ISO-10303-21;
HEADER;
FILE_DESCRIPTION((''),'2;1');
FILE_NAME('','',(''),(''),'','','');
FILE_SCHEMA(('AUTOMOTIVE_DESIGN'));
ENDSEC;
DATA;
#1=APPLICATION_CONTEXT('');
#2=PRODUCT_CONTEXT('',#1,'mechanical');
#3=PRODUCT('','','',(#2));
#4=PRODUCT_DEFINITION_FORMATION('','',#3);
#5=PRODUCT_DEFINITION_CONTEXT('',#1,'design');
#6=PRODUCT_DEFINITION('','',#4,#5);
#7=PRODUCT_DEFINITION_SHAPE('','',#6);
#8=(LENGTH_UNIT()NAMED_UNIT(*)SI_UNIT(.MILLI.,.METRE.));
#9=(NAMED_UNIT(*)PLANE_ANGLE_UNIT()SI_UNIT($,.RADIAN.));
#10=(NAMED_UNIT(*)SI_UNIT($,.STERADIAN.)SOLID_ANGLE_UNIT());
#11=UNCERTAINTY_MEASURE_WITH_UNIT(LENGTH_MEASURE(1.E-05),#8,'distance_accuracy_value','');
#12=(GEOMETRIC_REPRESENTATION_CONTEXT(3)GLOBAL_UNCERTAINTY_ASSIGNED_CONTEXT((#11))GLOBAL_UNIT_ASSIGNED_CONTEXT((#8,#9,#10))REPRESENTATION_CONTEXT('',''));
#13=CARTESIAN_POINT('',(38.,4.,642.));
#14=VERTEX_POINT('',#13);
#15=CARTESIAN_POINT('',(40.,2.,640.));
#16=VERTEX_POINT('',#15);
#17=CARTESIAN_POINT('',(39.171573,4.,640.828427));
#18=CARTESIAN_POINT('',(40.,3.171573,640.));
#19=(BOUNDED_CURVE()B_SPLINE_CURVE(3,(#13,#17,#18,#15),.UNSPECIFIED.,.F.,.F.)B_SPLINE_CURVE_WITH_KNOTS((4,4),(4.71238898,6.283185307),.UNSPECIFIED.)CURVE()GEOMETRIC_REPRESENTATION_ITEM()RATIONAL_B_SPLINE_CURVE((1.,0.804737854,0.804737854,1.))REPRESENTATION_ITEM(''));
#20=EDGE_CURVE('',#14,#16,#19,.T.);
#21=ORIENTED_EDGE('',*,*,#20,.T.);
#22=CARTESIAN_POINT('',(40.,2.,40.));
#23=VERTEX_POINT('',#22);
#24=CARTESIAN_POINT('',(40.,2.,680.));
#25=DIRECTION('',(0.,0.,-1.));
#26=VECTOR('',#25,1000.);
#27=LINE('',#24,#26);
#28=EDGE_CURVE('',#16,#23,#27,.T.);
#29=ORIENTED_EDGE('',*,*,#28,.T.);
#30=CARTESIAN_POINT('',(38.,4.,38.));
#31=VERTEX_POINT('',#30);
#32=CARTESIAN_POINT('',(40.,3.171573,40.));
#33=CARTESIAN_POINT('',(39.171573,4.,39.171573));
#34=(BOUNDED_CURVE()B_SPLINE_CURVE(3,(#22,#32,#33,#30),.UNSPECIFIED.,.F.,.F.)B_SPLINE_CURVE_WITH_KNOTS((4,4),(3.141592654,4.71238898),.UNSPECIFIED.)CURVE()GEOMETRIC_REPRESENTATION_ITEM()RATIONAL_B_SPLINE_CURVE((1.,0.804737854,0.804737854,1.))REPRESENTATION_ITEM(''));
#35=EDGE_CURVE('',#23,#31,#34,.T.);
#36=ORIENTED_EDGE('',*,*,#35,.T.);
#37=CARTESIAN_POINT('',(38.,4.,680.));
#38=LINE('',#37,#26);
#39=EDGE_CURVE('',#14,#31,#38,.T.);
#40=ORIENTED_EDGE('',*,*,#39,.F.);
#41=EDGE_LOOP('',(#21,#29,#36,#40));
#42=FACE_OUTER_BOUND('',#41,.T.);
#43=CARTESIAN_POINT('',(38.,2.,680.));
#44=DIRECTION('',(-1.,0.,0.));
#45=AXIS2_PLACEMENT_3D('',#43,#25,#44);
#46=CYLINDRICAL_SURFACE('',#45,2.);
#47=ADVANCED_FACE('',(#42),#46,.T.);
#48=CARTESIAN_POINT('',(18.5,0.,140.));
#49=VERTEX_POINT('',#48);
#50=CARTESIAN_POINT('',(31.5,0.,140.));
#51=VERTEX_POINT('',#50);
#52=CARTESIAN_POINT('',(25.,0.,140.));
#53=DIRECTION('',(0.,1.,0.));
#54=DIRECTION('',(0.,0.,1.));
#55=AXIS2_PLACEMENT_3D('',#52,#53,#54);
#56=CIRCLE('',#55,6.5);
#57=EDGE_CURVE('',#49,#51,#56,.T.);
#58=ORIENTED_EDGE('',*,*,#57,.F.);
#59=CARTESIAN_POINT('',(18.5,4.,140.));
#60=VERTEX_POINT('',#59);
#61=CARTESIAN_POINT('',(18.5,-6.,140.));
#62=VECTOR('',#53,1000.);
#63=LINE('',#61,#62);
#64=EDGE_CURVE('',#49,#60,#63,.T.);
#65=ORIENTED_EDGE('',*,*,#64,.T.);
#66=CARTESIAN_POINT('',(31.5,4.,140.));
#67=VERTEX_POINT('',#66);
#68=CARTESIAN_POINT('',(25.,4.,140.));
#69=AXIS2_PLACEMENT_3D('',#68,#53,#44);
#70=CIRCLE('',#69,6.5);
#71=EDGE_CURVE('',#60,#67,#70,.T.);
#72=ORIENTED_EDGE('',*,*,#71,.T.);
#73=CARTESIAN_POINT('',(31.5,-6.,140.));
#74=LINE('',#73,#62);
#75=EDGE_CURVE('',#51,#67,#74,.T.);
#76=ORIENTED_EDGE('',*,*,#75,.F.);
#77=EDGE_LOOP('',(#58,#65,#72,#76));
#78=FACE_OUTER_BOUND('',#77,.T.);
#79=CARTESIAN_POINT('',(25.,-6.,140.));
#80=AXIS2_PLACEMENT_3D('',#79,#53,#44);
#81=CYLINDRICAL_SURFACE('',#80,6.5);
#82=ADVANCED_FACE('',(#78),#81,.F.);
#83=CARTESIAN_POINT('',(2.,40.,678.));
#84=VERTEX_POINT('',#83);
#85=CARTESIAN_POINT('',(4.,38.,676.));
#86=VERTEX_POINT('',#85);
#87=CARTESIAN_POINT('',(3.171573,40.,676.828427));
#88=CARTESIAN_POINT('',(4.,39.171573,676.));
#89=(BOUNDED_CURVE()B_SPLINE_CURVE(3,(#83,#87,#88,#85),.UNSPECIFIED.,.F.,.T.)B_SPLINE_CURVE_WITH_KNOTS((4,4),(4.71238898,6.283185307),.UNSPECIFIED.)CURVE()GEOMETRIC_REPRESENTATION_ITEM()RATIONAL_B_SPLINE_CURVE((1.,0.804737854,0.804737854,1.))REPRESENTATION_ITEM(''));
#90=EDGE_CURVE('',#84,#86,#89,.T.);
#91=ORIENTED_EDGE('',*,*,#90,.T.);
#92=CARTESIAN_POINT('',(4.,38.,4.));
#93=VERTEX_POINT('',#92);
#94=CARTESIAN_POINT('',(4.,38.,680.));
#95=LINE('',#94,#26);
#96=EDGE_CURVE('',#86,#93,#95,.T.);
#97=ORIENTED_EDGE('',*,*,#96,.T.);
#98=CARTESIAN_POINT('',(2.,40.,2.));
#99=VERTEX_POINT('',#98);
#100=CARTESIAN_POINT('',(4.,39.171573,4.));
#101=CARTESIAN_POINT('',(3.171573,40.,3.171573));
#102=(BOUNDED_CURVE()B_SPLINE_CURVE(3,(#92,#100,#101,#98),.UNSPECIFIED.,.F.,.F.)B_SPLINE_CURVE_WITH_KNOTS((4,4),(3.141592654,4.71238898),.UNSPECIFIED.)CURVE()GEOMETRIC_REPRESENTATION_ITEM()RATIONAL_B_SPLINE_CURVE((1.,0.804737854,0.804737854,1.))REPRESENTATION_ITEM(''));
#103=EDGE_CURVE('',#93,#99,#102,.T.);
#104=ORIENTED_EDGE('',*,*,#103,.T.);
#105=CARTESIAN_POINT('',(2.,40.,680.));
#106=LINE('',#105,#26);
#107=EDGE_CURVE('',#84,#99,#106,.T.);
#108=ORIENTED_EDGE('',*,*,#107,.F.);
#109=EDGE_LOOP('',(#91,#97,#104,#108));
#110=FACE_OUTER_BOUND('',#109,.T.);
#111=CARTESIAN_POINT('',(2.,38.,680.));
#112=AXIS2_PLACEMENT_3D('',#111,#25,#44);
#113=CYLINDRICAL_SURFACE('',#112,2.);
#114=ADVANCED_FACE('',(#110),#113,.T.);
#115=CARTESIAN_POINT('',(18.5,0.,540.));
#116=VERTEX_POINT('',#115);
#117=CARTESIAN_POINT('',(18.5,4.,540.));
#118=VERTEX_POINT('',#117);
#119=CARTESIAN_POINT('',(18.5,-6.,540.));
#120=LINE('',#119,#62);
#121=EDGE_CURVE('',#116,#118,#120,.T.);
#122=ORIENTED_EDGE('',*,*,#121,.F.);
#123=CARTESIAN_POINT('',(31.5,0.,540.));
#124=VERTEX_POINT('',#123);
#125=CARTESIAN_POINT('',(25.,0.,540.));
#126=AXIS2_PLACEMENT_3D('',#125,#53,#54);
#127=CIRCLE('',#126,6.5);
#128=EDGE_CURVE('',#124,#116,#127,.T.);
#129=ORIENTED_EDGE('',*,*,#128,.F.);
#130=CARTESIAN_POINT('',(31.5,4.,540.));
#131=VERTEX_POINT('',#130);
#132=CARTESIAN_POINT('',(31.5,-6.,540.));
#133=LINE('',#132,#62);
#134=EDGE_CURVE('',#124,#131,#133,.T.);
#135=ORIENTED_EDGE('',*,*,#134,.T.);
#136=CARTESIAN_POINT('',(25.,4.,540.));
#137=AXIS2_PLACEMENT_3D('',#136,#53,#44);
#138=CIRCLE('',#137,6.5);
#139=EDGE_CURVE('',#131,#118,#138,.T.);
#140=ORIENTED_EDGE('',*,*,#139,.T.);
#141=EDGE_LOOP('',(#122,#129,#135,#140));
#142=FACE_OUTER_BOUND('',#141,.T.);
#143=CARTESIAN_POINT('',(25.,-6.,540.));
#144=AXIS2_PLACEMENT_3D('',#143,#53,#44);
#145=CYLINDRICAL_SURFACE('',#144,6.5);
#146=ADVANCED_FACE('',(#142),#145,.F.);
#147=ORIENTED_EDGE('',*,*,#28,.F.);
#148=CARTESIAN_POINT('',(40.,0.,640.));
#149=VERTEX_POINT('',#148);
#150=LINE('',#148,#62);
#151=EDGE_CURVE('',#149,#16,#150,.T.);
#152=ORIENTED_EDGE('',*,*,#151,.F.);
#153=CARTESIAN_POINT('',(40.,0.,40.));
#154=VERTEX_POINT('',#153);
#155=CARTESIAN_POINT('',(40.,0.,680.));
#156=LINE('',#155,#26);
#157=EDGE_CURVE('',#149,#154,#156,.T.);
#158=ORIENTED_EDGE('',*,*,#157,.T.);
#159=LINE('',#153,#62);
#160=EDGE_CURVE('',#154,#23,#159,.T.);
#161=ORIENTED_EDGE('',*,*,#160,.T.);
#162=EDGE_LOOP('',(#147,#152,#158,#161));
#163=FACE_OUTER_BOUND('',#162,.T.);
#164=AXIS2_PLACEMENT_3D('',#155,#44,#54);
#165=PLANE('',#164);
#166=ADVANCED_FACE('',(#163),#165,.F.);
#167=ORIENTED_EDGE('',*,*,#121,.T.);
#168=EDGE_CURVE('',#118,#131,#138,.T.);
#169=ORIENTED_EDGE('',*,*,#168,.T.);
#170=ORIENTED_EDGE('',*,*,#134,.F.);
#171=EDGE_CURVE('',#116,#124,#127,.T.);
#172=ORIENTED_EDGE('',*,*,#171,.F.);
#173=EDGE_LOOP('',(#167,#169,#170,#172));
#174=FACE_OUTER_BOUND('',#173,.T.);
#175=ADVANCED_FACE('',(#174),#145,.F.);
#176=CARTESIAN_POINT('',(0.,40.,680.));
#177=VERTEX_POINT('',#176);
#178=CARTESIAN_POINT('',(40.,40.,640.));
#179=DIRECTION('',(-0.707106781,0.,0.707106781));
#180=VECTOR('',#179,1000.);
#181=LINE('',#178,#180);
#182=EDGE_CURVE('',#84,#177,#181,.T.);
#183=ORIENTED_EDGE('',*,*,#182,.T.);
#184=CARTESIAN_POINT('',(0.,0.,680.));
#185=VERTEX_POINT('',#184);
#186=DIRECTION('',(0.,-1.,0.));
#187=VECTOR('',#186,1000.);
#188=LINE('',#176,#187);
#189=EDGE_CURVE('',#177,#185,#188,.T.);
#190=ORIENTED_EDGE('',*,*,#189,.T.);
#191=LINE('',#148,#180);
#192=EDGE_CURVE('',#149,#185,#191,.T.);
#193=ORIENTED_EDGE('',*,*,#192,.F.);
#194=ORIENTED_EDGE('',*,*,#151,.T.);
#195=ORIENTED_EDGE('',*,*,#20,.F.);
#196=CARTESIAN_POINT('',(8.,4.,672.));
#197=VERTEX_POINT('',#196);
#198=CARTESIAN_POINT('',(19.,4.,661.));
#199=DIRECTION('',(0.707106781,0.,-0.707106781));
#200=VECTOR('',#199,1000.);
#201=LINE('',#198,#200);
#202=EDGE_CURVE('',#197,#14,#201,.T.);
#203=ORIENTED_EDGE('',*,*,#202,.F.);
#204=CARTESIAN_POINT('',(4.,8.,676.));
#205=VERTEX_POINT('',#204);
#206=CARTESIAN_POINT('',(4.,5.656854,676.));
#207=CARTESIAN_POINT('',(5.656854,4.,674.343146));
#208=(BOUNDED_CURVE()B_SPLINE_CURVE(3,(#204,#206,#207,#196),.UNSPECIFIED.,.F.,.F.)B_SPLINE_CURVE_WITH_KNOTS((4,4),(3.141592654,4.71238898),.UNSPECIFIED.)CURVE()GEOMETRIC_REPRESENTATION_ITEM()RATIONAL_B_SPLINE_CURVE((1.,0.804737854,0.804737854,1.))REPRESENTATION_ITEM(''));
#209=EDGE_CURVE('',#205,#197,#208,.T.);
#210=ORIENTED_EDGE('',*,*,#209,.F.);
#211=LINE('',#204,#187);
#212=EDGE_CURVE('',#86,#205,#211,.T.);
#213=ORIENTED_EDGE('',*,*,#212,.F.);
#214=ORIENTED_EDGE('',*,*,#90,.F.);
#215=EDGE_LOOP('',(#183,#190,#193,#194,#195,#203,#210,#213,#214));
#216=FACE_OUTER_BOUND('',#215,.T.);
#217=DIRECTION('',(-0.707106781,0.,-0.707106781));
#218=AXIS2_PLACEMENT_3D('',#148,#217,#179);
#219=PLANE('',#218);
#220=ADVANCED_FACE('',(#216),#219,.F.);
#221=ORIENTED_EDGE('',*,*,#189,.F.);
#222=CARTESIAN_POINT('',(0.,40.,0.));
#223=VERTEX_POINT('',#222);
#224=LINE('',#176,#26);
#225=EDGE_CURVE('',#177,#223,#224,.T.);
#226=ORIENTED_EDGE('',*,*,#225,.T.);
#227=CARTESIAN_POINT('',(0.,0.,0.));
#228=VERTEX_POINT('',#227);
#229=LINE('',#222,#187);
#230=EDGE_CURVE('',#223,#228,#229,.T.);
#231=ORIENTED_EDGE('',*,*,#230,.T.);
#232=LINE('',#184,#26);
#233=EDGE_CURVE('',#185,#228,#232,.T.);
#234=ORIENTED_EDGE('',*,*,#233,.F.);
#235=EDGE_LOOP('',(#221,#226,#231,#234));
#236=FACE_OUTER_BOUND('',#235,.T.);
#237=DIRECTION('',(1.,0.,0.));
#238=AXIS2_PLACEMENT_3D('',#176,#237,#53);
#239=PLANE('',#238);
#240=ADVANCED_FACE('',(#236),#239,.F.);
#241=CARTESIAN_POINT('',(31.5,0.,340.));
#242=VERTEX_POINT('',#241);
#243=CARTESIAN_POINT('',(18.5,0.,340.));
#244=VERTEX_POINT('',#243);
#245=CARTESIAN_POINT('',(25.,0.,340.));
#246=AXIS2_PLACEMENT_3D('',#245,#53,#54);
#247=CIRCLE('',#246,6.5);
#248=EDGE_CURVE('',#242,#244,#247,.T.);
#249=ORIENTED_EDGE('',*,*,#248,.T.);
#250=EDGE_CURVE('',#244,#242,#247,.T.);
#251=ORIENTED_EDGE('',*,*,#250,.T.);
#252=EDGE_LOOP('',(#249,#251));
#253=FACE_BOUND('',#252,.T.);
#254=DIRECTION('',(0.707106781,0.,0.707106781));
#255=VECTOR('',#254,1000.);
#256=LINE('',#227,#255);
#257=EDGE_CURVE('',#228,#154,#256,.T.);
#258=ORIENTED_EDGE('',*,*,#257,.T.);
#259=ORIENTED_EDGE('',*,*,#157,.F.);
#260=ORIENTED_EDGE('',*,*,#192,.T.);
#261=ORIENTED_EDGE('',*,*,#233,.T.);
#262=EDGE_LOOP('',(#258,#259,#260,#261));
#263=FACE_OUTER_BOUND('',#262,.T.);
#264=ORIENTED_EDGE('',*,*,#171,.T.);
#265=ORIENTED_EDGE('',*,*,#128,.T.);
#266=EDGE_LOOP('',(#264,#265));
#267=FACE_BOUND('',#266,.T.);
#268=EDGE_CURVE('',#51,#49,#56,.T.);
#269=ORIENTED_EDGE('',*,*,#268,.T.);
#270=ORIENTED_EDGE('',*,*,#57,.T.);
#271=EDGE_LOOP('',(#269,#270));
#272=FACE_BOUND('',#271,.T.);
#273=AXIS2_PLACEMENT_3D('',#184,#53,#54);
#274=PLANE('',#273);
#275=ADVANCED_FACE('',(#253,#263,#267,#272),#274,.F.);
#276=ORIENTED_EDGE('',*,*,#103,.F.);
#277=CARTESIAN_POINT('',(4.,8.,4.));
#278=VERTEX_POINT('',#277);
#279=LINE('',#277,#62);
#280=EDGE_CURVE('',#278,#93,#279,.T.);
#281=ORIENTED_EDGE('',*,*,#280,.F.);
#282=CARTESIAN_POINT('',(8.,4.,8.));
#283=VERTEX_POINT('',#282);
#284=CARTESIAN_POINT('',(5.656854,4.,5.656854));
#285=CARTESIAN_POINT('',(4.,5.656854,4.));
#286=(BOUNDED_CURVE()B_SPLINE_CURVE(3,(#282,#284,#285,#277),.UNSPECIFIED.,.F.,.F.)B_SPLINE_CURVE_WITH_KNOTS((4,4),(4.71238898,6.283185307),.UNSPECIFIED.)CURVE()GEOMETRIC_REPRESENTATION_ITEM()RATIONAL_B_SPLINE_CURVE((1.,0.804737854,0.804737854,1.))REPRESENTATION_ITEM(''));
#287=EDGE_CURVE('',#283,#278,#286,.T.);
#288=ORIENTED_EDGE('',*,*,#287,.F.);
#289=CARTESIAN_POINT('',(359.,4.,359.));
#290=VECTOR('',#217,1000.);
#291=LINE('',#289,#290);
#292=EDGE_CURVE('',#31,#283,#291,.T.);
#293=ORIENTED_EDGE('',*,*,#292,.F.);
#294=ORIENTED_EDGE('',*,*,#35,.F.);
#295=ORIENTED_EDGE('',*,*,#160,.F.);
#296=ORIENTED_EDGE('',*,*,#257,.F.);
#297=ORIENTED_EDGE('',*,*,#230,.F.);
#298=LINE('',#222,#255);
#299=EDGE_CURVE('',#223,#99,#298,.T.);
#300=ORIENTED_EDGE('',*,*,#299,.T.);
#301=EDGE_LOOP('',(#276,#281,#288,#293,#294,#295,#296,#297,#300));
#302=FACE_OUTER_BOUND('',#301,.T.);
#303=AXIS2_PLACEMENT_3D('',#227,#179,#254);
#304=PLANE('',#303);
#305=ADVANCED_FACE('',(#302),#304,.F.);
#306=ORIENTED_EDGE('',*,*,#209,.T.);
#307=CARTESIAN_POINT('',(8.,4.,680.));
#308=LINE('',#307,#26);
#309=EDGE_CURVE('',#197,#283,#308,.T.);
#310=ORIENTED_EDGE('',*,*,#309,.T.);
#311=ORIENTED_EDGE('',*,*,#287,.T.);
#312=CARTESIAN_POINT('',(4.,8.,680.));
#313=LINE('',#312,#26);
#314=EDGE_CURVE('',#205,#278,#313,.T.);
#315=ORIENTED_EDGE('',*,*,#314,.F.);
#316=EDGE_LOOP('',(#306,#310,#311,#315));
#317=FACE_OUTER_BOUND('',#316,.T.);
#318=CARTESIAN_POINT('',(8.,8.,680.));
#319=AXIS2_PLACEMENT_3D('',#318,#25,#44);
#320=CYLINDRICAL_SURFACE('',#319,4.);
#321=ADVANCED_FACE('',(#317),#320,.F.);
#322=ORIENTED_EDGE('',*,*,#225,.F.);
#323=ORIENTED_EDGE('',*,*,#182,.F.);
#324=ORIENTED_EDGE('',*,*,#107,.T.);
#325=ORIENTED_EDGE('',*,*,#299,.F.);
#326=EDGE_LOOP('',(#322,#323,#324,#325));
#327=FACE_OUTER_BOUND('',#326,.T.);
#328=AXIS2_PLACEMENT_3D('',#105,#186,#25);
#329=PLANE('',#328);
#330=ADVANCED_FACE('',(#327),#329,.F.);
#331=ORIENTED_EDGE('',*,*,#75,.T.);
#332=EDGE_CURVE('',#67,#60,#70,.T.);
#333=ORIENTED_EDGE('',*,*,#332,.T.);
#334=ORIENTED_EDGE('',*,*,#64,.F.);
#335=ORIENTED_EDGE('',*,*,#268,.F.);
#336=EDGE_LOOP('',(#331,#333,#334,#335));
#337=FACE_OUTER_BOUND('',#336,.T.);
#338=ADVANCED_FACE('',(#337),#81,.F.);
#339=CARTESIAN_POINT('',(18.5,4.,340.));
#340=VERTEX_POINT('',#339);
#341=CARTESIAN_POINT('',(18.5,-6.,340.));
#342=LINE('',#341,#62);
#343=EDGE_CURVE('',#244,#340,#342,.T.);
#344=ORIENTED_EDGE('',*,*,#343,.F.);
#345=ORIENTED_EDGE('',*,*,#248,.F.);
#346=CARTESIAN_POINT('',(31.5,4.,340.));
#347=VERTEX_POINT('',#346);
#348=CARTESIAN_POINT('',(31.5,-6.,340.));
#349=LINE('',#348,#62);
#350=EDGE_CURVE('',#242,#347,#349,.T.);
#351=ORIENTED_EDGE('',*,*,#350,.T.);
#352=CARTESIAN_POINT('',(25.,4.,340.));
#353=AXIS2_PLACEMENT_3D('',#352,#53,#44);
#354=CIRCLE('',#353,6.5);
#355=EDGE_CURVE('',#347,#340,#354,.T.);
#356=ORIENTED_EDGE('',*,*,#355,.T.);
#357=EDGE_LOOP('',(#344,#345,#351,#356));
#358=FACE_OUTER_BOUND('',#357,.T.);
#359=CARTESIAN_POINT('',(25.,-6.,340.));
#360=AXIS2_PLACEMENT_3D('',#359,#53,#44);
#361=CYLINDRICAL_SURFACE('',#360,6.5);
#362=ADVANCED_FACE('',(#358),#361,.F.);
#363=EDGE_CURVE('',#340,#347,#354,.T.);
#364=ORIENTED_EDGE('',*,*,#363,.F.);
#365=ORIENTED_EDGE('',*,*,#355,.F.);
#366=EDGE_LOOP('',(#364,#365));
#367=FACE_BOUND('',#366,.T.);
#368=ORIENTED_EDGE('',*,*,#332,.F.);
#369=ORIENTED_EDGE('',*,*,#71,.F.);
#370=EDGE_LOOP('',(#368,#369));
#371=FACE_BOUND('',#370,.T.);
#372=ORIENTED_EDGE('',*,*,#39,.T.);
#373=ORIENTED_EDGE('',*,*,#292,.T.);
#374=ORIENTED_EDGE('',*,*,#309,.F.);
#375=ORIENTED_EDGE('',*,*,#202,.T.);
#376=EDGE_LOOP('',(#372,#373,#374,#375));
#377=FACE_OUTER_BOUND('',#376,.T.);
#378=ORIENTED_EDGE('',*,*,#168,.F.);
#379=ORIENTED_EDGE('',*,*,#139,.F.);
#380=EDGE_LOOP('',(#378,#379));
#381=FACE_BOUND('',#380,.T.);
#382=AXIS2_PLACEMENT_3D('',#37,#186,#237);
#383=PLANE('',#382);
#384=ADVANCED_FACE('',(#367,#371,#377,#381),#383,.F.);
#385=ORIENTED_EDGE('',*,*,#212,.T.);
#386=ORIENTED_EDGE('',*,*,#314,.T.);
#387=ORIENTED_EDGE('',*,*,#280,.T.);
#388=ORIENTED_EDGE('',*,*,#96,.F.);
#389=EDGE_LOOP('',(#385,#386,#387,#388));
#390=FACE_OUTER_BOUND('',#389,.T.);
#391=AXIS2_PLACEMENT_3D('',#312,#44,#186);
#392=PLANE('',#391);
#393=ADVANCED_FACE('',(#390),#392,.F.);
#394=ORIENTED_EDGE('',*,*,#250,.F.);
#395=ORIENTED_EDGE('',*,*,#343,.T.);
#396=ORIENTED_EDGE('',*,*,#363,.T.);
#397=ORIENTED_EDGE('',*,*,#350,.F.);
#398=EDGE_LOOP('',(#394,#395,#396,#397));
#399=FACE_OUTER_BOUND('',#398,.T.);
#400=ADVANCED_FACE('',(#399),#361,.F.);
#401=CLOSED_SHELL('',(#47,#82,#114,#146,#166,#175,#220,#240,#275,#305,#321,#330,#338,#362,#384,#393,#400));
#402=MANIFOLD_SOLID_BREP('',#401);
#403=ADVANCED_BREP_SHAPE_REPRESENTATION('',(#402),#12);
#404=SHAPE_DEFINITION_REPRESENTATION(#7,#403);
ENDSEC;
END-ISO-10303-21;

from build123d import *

# Parameters (mm, degrees)
BOSS_EXTRUDE1_DEPTH     = 680
CUT_EXTRUDE1_DEPTH      = 683.126088051
CUT_EXTRUDE1_DEPTH_BACK = 683.126088051
SKETCH3_R               = 6.5
CUT_EXTRUDE2_DEPTH      = 10


with BuildPart() as part:
    # Sketch1 → Boss-Extrude1 (new body)
    with BuildSketch(Plane.XY):
        with BuildLine():
            Line((0, 40), (0, 0))
            Line((0, 0), (40, 0))
            Line((40, 0), (40, 2))
            ThreePointArc((40, 2), (39.414213562, 3.414213562), (38, 4))
            Line((38, 4), (8, 4))
            ThreePointArc((8, 4), (5.171572875, 5.171572875), (4, 8))
            Line((4, 8), (4, 38))
            ThreePointArc((4, 38), (3.414213562, 39.414213562), (2, 40))
            Line((2, 40), (0, 40))
        make_face()
    extrude(amount=BOSS_EXTRUDE1_DEPTH)

    # Sketch2 → Cut-Extrude1 (cut, two sides: drawn at the far end of the back side and taken through both)
    with BuildSketch(Plane(origin=(0, 4, 0), x_dir=(1, 0, 0), z_dir=(0, 1, 0)).offset(-CUT_EXTRUDE1_DEPTH_BACK)):
        Polygon((0, 0), (40, -40), (40, 0), align=None)
        Polygon((0, -680), (40, -680), (40, -640), align=None)
    extrude(amount=CUT_EXTRUDE1_DEPTH + CUT_EXTRUDE1_DEPTH_BACK, mode=Mode.SUBTRACT)

    # Sketch3 → Cut-Extrude2 (cut)
    with BuildSketch(Plane(origin=(0, 4, 0), x_dir=(1, 0, 0), z_dir=(0, 1, 0))):
        with Locations(Location((25, -140, 0), (0, 0, 180))):
            Circle(SKETCH3_R)
        with Locations(Location((25, -340, 0), (0, 0, 180))):
            Circle(SKETCH3_R)
        with Locations(Location((25, -540, 0), (0, 0, 180))):
            Circle(SKETCH3_R)
    extrude(amount=-CUT_EXTRUDE2_DEPTH, mode=Mode.SUBTRACT)


solid = part.part
